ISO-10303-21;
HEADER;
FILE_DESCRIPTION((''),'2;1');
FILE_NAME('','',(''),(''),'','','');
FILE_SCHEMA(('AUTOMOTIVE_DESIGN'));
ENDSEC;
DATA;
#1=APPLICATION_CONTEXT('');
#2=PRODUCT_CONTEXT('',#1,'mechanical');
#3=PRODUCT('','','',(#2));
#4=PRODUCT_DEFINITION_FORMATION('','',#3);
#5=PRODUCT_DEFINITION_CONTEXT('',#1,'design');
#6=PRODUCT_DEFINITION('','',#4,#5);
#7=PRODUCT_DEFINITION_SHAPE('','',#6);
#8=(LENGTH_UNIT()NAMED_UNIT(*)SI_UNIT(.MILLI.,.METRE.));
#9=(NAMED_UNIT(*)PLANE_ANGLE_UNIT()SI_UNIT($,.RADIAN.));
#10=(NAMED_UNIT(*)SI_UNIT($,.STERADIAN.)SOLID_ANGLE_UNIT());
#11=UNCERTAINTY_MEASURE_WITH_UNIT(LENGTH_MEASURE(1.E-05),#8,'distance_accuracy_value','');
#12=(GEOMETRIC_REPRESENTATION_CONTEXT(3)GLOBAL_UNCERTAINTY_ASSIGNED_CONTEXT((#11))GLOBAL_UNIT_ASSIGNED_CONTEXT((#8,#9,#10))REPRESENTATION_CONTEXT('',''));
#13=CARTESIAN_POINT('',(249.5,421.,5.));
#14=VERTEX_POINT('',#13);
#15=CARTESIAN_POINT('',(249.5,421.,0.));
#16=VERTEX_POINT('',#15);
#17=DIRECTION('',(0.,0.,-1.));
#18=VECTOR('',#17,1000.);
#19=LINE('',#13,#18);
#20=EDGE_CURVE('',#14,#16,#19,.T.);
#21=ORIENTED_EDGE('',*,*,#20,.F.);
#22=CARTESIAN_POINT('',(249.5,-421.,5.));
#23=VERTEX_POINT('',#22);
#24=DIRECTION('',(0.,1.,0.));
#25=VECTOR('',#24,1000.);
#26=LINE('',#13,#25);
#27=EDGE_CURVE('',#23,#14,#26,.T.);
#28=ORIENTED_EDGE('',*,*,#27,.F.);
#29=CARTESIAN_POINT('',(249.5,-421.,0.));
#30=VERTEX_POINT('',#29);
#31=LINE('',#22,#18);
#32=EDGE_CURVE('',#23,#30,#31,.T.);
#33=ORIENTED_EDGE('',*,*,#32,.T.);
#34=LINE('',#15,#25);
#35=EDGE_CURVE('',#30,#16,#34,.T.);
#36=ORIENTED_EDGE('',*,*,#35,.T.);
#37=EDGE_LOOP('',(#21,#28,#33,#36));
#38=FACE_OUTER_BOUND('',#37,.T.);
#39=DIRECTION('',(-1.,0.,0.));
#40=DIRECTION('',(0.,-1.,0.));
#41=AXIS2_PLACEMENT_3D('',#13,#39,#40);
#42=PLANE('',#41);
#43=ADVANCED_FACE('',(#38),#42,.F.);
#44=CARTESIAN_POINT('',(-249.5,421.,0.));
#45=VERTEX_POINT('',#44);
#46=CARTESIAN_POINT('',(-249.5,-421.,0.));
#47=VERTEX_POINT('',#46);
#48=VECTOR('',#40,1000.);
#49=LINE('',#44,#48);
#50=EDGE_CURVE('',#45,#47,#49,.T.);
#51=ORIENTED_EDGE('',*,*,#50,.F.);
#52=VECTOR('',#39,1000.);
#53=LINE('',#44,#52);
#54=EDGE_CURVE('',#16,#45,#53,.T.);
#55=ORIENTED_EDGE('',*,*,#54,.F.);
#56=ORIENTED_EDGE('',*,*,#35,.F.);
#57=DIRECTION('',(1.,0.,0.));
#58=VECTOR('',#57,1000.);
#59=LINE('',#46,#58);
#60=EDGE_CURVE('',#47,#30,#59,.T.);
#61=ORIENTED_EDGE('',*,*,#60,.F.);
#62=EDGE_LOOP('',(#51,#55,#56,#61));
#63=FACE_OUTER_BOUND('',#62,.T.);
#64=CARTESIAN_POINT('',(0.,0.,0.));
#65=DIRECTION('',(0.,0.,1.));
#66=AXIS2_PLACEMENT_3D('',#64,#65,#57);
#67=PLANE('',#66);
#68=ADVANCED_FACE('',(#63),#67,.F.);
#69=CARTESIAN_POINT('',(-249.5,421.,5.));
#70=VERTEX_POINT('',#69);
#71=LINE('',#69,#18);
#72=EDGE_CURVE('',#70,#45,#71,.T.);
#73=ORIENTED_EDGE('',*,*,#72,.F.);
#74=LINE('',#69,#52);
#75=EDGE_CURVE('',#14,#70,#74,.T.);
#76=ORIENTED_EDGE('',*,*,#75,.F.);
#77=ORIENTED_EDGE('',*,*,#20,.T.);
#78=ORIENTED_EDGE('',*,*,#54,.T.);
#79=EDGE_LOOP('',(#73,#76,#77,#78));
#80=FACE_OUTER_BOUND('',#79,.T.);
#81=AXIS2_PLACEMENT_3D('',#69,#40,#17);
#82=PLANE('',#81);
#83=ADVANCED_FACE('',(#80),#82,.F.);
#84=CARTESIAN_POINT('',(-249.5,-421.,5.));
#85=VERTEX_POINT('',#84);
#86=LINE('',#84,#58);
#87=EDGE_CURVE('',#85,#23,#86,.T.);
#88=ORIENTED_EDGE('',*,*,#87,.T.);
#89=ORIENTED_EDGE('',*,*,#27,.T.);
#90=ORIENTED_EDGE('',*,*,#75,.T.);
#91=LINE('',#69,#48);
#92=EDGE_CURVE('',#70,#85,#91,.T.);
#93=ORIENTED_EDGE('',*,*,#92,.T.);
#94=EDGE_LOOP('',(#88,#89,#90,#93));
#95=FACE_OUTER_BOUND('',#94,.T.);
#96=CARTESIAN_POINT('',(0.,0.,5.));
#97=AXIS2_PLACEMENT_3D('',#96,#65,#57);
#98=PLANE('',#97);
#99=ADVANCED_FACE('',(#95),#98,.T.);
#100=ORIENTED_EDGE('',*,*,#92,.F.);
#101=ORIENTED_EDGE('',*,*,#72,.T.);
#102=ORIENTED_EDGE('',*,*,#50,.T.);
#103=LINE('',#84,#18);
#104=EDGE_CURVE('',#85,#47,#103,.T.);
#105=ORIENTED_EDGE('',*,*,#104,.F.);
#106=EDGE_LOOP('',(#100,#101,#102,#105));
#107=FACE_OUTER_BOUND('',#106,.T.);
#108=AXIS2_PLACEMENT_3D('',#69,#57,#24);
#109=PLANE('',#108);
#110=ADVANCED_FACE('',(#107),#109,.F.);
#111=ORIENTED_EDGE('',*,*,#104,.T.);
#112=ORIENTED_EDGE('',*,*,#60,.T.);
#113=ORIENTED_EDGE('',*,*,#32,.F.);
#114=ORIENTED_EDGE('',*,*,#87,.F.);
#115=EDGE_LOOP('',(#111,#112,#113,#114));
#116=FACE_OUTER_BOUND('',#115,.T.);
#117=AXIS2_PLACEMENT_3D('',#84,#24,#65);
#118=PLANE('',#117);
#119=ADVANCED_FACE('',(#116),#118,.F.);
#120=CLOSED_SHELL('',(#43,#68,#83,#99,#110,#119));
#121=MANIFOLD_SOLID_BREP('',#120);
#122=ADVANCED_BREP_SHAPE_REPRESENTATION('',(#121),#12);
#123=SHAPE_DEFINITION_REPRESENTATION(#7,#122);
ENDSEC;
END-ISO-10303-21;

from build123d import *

# Parameters (mm, degrees)
SKETCH_1_W      = 499
SKETCH_1_H      = 842
EXTRUDE_1_DEPTH = 5


with BuildPart() as part:
    # 草图1 → 凸台-拉伸1 (new body)
    with BuildSketch(Plane.XY):
        Rectangle(SKETCH_1_W, SKETCH_1_H)
    extrude(amount=EXTRUDE_1_DEPTH)


solid = part.part
